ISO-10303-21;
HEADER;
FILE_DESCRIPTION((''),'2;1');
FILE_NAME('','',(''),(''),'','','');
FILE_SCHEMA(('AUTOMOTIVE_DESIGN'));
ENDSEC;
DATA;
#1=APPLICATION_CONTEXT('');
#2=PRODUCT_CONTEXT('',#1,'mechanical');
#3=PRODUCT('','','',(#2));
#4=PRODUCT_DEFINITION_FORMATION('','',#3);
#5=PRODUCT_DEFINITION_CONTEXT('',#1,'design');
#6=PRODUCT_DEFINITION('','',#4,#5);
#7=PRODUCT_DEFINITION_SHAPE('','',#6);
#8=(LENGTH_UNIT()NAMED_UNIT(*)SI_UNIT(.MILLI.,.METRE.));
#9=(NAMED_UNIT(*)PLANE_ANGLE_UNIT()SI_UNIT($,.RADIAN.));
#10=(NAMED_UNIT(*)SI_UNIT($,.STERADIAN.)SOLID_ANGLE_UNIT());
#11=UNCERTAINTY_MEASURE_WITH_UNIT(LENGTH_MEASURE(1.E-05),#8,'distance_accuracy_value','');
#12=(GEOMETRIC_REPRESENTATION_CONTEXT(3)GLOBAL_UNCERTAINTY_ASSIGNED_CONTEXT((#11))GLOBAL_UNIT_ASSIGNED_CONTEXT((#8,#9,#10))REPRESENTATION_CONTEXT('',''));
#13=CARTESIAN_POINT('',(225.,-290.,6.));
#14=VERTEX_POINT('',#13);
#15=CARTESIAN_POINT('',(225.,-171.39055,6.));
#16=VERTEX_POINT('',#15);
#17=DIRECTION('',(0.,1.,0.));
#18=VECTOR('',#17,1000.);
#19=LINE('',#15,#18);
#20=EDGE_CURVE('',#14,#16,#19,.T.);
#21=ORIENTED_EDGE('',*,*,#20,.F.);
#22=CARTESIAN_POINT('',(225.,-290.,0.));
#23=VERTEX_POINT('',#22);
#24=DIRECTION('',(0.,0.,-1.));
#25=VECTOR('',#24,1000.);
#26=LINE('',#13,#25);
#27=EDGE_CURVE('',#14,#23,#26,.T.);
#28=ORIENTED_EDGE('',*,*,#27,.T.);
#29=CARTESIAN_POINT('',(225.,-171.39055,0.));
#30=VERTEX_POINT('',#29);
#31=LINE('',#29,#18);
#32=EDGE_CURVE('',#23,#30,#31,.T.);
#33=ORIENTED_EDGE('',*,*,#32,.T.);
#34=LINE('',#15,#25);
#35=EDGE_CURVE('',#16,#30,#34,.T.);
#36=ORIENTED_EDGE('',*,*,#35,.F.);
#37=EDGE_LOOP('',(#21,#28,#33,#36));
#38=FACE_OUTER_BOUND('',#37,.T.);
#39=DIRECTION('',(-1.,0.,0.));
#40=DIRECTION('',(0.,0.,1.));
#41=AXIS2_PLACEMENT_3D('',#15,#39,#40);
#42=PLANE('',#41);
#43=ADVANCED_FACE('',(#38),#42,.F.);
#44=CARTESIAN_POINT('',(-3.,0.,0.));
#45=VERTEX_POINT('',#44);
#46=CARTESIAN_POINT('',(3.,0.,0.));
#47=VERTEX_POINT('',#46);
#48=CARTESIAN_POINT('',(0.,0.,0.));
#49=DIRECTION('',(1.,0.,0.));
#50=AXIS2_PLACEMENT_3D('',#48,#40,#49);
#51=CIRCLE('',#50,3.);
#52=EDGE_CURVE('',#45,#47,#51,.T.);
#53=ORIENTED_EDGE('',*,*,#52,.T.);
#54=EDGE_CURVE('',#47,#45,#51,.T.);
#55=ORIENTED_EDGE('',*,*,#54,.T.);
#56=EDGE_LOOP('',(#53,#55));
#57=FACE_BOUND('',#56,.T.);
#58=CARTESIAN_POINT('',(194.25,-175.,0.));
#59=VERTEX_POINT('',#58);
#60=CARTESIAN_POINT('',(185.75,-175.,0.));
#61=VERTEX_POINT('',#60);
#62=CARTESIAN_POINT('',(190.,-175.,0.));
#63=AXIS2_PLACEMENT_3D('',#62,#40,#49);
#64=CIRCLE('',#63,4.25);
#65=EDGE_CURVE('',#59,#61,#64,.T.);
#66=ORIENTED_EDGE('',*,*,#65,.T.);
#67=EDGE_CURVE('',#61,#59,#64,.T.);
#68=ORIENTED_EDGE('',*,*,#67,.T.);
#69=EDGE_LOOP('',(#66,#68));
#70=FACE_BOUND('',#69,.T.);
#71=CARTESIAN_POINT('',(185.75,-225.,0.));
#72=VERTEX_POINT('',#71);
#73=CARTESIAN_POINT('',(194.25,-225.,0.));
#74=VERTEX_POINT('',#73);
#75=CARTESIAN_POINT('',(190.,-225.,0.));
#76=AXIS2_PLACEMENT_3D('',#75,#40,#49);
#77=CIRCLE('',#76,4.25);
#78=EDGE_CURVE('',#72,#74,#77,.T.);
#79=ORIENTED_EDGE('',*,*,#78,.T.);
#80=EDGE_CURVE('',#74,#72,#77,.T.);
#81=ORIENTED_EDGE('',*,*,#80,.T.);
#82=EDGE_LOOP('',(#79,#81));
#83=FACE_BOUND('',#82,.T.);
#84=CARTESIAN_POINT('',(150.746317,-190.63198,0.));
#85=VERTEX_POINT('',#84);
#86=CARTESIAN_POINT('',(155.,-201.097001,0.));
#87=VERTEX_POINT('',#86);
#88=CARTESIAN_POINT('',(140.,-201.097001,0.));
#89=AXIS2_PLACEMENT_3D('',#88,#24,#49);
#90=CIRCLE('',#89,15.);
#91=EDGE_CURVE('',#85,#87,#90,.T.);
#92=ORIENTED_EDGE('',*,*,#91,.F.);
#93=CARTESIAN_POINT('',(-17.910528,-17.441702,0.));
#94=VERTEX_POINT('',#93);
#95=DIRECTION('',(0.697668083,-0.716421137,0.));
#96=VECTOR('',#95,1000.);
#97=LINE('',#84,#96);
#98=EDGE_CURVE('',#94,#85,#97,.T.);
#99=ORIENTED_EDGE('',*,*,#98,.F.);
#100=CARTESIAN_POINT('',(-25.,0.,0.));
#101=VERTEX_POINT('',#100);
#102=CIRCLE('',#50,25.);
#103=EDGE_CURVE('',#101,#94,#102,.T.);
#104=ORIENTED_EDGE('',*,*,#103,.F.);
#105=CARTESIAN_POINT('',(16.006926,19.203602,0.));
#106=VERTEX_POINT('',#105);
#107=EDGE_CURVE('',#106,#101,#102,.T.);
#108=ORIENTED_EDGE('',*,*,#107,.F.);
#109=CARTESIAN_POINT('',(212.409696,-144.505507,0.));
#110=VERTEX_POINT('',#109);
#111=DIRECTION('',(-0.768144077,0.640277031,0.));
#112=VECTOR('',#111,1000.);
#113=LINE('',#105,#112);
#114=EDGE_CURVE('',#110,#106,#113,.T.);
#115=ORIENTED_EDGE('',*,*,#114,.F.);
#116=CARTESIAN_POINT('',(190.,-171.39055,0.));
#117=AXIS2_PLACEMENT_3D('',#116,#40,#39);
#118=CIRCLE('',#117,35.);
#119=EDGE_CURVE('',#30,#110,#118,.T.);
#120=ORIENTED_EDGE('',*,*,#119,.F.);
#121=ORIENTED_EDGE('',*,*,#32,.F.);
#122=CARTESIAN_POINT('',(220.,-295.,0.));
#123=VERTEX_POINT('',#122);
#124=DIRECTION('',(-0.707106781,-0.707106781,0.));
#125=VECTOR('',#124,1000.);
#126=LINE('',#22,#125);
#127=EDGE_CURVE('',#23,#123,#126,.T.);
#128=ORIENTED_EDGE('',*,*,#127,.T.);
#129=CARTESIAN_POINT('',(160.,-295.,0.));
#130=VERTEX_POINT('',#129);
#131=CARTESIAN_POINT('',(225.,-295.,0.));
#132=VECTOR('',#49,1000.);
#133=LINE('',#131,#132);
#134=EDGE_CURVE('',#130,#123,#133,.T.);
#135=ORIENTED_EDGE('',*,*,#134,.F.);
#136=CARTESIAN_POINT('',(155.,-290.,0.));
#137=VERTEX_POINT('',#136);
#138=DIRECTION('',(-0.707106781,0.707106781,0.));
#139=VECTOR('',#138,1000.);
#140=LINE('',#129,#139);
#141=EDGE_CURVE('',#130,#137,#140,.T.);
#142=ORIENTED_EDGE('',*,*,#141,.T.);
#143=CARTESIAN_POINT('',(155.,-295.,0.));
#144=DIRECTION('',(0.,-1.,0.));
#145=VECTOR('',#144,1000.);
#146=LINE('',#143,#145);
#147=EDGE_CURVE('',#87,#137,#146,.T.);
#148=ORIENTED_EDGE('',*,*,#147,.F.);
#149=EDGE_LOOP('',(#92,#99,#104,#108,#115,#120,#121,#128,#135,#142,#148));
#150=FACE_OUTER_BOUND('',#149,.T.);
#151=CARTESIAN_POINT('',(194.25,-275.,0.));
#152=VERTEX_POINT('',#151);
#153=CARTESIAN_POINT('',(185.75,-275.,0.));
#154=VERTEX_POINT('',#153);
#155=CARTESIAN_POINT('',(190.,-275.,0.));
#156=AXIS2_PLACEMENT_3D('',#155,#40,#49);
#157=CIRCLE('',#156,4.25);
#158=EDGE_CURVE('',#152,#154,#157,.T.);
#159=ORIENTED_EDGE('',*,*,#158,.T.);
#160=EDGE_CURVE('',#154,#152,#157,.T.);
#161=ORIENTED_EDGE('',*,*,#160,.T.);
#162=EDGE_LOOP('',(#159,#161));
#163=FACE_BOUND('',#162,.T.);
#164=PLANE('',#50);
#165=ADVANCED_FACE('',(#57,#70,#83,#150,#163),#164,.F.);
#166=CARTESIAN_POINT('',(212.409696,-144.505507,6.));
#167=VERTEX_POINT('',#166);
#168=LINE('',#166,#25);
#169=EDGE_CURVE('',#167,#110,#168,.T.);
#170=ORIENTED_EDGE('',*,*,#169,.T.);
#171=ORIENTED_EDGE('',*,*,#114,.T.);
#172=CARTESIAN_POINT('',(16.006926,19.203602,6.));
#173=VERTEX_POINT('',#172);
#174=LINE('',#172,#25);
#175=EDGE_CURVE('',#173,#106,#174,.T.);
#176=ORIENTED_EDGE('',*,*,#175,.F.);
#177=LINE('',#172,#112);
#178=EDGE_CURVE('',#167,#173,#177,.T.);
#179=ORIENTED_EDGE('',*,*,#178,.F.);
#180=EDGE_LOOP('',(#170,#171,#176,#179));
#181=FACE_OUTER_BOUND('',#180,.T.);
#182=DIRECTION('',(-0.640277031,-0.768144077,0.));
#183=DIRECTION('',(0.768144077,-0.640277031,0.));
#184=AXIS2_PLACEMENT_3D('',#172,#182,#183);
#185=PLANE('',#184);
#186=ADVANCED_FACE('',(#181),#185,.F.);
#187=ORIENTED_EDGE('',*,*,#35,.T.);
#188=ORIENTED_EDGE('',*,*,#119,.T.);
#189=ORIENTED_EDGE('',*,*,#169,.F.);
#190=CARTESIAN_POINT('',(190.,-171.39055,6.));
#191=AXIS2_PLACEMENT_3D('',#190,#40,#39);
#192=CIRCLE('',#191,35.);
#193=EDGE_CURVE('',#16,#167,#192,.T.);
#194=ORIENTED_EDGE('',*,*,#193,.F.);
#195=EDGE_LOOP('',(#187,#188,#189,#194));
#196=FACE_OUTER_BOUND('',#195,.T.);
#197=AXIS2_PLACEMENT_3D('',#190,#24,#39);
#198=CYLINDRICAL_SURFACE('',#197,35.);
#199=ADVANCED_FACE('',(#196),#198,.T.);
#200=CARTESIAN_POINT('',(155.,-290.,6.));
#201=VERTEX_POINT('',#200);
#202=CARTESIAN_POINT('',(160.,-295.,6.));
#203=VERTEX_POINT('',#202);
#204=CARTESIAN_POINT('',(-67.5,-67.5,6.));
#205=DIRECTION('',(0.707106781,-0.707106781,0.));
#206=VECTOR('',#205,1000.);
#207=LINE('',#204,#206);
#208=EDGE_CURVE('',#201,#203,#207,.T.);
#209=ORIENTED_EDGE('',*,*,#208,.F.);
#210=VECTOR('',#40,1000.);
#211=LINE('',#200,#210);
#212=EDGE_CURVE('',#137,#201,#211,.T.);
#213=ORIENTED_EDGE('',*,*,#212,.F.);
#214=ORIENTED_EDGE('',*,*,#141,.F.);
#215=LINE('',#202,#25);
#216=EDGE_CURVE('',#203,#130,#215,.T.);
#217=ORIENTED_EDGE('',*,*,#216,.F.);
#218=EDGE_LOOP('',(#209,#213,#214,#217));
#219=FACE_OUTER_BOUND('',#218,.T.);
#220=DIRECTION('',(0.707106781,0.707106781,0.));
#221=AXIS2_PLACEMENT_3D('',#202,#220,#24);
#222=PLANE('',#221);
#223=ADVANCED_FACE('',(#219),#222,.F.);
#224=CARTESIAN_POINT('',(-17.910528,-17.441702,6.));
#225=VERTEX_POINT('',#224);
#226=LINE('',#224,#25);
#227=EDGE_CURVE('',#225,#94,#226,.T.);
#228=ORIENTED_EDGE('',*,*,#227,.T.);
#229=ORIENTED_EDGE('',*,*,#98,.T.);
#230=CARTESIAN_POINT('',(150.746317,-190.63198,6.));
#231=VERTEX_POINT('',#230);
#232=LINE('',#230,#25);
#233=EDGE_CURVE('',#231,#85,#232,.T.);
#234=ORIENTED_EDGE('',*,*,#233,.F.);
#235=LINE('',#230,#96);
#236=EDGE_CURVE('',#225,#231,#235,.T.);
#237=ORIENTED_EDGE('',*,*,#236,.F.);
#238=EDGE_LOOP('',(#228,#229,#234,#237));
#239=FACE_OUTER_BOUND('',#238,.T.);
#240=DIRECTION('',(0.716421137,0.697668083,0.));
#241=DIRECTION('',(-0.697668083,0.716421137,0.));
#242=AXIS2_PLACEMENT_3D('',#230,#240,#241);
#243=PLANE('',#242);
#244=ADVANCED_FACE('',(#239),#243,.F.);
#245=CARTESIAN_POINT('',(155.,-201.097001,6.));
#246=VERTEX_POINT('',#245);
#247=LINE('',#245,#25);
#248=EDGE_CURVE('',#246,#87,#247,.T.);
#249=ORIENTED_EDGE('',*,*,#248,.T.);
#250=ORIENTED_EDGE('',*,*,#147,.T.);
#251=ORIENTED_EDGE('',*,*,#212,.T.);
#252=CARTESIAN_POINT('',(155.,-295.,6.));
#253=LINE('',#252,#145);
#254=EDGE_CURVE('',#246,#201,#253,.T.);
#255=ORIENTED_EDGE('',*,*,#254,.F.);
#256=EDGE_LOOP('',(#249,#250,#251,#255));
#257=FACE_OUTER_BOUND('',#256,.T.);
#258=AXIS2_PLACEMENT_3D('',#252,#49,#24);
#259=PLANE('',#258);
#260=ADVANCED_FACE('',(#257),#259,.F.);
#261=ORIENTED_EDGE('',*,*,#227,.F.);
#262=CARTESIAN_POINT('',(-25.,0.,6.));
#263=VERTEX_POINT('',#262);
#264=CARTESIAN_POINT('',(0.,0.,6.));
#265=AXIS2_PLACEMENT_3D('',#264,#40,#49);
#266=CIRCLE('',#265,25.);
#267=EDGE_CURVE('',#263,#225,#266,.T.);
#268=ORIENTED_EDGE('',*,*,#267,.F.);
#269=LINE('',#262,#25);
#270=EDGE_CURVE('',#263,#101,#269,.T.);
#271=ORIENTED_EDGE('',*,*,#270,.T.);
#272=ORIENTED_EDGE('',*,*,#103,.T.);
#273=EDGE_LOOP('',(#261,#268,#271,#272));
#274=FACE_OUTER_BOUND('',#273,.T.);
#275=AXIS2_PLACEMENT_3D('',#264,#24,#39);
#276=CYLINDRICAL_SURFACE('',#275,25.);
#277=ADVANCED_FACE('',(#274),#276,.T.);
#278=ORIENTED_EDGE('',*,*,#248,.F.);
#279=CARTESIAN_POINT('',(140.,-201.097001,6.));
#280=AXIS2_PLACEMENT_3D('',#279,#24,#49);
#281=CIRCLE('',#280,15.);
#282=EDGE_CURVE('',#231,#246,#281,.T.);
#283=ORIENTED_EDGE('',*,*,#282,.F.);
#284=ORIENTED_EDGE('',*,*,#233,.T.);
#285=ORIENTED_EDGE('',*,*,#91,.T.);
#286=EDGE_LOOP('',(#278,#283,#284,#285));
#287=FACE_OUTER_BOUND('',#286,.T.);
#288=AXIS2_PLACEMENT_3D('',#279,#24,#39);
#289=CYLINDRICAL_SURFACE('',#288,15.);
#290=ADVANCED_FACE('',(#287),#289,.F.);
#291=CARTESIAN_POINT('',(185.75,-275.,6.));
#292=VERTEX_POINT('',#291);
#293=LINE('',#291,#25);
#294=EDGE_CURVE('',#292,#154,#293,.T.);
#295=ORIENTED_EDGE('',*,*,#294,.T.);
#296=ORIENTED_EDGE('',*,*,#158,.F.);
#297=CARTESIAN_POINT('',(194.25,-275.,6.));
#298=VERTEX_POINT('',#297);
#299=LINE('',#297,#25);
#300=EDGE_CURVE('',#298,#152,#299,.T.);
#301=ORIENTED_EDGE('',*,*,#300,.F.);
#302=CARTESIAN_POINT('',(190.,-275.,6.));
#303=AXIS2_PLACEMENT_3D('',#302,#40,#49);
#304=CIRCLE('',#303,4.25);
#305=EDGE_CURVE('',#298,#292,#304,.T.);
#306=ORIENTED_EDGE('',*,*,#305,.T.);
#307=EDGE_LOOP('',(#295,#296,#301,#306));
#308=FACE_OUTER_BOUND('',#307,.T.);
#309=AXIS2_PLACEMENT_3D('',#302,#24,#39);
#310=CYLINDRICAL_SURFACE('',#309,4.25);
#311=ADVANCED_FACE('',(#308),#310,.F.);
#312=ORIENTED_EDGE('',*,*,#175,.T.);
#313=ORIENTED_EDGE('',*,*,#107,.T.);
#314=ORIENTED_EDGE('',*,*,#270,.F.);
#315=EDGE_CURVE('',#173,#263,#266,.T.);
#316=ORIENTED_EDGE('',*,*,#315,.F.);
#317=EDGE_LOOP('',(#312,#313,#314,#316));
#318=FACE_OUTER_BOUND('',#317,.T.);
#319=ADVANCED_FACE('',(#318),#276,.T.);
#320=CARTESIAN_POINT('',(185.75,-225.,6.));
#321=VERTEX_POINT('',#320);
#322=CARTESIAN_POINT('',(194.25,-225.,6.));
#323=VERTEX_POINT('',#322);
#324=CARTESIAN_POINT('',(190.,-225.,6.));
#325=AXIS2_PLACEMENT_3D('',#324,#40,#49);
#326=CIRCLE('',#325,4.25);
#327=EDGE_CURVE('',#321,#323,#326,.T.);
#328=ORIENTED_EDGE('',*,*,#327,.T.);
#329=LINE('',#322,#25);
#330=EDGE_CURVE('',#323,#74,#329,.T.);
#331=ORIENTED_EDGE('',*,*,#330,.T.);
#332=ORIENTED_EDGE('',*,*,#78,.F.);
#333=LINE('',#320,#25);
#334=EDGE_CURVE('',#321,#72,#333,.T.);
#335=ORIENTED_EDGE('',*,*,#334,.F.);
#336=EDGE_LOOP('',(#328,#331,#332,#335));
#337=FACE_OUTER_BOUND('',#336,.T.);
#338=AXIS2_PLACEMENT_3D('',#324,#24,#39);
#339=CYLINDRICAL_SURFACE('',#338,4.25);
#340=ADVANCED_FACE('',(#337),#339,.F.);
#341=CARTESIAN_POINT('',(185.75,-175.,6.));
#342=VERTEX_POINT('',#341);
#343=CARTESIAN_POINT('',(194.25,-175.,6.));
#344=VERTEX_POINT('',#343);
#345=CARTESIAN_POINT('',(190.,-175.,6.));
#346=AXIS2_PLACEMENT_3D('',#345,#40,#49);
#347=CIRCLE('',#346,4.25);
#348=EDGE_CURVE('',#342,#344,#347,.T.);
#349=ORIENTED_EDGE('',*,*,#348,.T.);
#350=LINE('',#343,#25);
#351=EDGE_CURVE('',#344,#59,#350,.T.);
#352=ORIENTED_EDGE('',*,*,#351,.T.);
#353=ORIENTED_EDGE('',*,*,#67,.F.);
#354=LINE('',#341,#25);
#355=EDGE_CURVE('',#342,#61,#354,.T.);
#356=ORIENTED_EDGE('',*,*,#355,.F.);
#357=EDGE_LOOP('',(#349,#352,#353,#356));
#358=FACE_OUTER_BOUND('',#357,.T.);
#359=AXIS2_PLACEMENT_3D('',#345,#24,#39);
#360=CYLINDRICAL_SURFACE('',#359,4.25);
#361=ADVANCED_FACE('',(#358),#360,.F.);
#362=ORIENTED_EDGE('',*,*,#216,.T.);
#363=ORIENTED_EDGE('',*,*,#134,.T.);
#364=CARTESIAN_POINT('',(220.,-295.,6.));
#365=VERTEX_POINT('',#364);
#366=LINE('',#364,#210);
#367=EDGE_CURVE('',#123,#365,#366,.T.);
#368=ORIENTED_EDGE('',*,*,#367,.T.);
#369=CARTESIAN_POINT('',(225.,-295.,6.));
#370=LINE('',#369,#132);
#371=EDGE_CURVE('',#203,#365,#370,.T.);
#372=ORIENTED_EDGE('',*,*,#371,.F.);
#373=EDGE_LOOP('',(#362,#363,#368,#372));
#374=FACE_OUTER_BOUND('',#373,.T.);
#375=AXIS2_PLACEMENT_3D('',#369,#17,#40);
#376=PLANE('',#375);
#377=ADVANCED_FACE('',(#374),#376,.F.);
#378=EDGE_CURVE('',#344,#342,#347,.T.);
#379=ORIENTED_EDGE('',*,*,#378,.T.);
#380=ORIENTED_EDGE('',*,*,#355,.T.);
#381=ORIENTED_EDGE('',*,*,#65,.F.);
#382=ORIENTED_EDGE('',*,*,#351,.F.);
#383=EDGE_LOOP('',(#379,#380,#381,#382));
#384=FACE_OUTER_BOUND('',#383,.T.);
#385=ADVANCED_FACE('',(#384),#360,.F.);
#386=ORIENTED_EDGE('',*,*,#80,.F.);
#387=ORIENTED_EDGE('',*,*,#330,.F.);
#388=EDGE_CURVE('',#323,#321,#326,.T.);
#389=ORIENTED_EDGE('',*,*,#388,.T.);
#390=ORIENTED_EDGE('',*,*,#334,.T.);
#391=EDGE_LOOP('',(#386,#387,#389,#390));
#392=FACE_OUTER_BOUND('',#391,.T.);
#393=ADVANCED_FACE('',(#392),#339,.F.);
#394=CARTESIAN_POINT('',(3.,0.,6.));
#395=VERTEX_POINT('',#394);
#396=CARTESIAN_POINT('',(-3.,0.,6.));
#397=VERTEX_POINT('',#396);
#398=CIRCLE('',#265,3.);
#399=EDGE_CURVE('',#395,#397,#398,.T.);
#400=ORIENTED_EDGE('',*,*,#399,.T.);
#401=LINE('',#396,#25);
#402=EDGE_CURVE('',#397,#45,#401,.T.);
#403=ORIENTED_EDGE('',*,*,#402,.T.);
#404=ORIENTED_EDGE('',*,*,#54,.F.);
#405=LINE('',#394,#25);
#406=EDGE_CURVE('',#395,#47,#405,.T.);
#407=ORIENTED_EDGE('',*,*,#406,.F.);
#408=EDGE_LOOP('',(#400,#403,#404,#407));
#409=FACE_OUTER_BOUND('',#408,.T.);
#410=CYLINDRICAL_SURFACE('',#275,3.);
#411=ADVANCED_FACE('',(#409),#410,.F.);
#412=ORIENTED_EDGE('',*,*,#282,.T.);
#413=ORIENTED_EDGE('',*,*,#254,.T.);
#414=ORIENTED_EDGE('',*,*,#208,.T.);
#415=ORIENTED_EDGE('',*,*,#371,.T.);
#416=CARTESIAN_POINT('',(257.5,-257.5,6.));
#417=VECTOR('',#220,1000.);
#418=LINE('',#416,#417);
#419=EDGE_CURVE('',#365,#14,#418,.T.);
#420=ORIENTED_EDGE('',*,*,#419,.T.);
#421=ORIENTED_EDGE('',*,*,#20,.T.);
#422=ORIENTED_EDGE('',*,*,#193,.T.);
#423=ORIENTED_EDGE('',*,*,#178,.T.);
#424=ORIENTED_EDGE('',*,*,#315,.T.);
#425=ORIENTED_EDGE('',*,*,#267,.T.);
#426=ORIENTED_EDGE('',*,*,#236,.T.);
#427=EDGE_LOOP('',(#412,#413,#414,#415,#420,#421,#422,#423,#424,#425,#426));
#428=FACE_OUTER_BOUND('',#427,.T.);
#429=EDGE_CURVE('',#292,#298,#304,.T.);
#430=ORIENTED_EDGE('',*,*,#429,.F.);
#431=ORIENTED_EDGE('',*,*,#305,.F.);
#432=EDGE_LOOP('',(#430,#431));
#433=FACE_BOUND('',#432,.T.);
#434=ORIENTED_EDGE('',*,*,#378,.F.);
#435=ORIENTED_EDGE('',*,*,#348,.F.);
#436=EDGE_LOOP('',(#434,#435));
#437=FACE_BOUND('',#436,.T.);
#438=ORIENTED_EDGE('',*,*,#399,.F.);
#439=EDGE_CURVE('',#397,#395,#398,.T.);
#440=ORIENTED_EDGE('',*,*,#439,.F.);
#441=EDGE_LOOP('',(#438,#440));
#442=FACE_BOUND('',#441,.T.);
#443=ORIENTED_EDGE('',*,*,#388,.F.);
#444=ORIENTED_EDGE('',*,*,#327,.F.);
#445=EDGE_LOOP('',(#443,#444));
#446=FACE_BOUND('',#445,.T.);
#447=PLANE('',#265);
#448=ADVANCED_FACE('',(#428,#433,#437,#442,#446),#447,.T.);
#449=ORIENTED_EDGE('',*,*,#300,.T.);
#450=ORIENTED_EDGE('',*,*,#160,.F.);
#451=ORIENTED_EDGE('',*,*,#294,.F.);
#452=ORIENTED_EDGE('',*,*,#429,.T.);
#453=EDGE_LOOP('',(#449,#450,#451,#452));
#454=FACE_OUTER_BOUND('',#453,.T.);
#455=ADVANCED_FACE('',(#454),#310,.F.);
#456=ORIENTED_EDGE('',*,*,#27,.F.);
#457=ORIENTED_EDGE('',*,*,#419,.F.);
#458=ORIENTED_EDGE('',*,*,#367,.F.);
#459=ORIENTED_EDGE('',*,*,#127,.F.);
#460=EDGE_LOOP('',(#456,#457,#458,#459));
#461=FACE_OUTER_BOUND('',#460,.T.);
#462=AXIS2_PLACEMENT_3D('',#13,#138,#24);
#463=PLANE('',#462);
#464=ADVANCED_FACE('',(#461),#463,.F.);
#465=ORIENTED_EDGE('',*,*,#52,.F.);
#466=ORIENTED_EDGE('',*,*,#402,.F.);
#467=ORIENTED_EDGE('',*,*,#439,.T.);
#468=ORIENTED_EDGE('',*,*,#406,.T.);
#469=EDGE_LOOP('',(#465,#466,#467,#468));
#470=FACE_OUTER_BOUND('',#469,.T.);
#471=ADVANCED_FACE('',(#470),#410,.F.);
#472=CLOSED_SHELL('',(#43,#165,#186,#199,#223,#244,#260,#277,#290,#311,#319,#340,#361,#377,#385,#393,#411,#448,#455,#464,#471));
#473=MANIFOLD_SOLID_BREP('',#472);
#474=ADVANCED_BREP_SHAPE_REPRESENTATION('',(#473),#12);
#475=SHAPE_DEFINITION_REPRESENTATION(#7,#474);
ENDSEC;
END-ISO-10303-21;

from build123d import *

# Parameters (mm, degrees)
SKETCH_1_R      = 3
SKETCH_1_R_2    = 4.25
EXTRUDE_1_DEPTH = 6
CHAMFER_1_SIZE  = 5


with BuildPart() as part:
    # 草图1 → 凸台-拉伸1 (new body)
    with BuildSketch(Plane.XY):
        with BuildLine():
            Line((16.006925776, 19.203601933), (212.409696086, -144.505507303))
            ThreePointArc((212.409696086, -144.505507303), (221.696524755, -156.547022178), (225, -171.390550009))
            Line((225, -171.390550009), (225, -295))
            Line((225, -295), (155, -295))
            Line((155, -295), (155, -201.097000919))
            ThreePointArc((155, -201.097000919), (153.895948255, -195.4487603), (150.746317055, -190.631979669))
            Line((150.746317055, -190.631979669), (-17.910528426, -17.441702082))
            ThreePointArc((-17.910528426, -17.441702082), (-18.347356822, 16.981592907), (16.006925776, 19.203601933))
        make_face()
        Circle(SKETCH_1_R, mode=Mode.SUBTRACT)
        with Locations((190, -275)):
            Circle(SKETCH_1_R_2, mode=Mode.SUBTRACT)
        with Locations((190, -225)):
            Circle(SKETCH_1_R_2, mode=Mode.SUBTRACT)
        with Locations((190, -175)):
            Circle(SKETCH_1_R_2, mode=Mode.SUBTRACT)
    extrude(amount=EXTRUDE_1_DEPTH)

    # 倒角1
    chamfer_1_edges = [part.edges().sort_by_distance(p)[0] for p in [
        (225, -295, 3),
        (155, -295, 3),
    ]]
    chamfer(chamfer_1_edges, length=CHAMFER_1_SIZE)


solid = part.part
